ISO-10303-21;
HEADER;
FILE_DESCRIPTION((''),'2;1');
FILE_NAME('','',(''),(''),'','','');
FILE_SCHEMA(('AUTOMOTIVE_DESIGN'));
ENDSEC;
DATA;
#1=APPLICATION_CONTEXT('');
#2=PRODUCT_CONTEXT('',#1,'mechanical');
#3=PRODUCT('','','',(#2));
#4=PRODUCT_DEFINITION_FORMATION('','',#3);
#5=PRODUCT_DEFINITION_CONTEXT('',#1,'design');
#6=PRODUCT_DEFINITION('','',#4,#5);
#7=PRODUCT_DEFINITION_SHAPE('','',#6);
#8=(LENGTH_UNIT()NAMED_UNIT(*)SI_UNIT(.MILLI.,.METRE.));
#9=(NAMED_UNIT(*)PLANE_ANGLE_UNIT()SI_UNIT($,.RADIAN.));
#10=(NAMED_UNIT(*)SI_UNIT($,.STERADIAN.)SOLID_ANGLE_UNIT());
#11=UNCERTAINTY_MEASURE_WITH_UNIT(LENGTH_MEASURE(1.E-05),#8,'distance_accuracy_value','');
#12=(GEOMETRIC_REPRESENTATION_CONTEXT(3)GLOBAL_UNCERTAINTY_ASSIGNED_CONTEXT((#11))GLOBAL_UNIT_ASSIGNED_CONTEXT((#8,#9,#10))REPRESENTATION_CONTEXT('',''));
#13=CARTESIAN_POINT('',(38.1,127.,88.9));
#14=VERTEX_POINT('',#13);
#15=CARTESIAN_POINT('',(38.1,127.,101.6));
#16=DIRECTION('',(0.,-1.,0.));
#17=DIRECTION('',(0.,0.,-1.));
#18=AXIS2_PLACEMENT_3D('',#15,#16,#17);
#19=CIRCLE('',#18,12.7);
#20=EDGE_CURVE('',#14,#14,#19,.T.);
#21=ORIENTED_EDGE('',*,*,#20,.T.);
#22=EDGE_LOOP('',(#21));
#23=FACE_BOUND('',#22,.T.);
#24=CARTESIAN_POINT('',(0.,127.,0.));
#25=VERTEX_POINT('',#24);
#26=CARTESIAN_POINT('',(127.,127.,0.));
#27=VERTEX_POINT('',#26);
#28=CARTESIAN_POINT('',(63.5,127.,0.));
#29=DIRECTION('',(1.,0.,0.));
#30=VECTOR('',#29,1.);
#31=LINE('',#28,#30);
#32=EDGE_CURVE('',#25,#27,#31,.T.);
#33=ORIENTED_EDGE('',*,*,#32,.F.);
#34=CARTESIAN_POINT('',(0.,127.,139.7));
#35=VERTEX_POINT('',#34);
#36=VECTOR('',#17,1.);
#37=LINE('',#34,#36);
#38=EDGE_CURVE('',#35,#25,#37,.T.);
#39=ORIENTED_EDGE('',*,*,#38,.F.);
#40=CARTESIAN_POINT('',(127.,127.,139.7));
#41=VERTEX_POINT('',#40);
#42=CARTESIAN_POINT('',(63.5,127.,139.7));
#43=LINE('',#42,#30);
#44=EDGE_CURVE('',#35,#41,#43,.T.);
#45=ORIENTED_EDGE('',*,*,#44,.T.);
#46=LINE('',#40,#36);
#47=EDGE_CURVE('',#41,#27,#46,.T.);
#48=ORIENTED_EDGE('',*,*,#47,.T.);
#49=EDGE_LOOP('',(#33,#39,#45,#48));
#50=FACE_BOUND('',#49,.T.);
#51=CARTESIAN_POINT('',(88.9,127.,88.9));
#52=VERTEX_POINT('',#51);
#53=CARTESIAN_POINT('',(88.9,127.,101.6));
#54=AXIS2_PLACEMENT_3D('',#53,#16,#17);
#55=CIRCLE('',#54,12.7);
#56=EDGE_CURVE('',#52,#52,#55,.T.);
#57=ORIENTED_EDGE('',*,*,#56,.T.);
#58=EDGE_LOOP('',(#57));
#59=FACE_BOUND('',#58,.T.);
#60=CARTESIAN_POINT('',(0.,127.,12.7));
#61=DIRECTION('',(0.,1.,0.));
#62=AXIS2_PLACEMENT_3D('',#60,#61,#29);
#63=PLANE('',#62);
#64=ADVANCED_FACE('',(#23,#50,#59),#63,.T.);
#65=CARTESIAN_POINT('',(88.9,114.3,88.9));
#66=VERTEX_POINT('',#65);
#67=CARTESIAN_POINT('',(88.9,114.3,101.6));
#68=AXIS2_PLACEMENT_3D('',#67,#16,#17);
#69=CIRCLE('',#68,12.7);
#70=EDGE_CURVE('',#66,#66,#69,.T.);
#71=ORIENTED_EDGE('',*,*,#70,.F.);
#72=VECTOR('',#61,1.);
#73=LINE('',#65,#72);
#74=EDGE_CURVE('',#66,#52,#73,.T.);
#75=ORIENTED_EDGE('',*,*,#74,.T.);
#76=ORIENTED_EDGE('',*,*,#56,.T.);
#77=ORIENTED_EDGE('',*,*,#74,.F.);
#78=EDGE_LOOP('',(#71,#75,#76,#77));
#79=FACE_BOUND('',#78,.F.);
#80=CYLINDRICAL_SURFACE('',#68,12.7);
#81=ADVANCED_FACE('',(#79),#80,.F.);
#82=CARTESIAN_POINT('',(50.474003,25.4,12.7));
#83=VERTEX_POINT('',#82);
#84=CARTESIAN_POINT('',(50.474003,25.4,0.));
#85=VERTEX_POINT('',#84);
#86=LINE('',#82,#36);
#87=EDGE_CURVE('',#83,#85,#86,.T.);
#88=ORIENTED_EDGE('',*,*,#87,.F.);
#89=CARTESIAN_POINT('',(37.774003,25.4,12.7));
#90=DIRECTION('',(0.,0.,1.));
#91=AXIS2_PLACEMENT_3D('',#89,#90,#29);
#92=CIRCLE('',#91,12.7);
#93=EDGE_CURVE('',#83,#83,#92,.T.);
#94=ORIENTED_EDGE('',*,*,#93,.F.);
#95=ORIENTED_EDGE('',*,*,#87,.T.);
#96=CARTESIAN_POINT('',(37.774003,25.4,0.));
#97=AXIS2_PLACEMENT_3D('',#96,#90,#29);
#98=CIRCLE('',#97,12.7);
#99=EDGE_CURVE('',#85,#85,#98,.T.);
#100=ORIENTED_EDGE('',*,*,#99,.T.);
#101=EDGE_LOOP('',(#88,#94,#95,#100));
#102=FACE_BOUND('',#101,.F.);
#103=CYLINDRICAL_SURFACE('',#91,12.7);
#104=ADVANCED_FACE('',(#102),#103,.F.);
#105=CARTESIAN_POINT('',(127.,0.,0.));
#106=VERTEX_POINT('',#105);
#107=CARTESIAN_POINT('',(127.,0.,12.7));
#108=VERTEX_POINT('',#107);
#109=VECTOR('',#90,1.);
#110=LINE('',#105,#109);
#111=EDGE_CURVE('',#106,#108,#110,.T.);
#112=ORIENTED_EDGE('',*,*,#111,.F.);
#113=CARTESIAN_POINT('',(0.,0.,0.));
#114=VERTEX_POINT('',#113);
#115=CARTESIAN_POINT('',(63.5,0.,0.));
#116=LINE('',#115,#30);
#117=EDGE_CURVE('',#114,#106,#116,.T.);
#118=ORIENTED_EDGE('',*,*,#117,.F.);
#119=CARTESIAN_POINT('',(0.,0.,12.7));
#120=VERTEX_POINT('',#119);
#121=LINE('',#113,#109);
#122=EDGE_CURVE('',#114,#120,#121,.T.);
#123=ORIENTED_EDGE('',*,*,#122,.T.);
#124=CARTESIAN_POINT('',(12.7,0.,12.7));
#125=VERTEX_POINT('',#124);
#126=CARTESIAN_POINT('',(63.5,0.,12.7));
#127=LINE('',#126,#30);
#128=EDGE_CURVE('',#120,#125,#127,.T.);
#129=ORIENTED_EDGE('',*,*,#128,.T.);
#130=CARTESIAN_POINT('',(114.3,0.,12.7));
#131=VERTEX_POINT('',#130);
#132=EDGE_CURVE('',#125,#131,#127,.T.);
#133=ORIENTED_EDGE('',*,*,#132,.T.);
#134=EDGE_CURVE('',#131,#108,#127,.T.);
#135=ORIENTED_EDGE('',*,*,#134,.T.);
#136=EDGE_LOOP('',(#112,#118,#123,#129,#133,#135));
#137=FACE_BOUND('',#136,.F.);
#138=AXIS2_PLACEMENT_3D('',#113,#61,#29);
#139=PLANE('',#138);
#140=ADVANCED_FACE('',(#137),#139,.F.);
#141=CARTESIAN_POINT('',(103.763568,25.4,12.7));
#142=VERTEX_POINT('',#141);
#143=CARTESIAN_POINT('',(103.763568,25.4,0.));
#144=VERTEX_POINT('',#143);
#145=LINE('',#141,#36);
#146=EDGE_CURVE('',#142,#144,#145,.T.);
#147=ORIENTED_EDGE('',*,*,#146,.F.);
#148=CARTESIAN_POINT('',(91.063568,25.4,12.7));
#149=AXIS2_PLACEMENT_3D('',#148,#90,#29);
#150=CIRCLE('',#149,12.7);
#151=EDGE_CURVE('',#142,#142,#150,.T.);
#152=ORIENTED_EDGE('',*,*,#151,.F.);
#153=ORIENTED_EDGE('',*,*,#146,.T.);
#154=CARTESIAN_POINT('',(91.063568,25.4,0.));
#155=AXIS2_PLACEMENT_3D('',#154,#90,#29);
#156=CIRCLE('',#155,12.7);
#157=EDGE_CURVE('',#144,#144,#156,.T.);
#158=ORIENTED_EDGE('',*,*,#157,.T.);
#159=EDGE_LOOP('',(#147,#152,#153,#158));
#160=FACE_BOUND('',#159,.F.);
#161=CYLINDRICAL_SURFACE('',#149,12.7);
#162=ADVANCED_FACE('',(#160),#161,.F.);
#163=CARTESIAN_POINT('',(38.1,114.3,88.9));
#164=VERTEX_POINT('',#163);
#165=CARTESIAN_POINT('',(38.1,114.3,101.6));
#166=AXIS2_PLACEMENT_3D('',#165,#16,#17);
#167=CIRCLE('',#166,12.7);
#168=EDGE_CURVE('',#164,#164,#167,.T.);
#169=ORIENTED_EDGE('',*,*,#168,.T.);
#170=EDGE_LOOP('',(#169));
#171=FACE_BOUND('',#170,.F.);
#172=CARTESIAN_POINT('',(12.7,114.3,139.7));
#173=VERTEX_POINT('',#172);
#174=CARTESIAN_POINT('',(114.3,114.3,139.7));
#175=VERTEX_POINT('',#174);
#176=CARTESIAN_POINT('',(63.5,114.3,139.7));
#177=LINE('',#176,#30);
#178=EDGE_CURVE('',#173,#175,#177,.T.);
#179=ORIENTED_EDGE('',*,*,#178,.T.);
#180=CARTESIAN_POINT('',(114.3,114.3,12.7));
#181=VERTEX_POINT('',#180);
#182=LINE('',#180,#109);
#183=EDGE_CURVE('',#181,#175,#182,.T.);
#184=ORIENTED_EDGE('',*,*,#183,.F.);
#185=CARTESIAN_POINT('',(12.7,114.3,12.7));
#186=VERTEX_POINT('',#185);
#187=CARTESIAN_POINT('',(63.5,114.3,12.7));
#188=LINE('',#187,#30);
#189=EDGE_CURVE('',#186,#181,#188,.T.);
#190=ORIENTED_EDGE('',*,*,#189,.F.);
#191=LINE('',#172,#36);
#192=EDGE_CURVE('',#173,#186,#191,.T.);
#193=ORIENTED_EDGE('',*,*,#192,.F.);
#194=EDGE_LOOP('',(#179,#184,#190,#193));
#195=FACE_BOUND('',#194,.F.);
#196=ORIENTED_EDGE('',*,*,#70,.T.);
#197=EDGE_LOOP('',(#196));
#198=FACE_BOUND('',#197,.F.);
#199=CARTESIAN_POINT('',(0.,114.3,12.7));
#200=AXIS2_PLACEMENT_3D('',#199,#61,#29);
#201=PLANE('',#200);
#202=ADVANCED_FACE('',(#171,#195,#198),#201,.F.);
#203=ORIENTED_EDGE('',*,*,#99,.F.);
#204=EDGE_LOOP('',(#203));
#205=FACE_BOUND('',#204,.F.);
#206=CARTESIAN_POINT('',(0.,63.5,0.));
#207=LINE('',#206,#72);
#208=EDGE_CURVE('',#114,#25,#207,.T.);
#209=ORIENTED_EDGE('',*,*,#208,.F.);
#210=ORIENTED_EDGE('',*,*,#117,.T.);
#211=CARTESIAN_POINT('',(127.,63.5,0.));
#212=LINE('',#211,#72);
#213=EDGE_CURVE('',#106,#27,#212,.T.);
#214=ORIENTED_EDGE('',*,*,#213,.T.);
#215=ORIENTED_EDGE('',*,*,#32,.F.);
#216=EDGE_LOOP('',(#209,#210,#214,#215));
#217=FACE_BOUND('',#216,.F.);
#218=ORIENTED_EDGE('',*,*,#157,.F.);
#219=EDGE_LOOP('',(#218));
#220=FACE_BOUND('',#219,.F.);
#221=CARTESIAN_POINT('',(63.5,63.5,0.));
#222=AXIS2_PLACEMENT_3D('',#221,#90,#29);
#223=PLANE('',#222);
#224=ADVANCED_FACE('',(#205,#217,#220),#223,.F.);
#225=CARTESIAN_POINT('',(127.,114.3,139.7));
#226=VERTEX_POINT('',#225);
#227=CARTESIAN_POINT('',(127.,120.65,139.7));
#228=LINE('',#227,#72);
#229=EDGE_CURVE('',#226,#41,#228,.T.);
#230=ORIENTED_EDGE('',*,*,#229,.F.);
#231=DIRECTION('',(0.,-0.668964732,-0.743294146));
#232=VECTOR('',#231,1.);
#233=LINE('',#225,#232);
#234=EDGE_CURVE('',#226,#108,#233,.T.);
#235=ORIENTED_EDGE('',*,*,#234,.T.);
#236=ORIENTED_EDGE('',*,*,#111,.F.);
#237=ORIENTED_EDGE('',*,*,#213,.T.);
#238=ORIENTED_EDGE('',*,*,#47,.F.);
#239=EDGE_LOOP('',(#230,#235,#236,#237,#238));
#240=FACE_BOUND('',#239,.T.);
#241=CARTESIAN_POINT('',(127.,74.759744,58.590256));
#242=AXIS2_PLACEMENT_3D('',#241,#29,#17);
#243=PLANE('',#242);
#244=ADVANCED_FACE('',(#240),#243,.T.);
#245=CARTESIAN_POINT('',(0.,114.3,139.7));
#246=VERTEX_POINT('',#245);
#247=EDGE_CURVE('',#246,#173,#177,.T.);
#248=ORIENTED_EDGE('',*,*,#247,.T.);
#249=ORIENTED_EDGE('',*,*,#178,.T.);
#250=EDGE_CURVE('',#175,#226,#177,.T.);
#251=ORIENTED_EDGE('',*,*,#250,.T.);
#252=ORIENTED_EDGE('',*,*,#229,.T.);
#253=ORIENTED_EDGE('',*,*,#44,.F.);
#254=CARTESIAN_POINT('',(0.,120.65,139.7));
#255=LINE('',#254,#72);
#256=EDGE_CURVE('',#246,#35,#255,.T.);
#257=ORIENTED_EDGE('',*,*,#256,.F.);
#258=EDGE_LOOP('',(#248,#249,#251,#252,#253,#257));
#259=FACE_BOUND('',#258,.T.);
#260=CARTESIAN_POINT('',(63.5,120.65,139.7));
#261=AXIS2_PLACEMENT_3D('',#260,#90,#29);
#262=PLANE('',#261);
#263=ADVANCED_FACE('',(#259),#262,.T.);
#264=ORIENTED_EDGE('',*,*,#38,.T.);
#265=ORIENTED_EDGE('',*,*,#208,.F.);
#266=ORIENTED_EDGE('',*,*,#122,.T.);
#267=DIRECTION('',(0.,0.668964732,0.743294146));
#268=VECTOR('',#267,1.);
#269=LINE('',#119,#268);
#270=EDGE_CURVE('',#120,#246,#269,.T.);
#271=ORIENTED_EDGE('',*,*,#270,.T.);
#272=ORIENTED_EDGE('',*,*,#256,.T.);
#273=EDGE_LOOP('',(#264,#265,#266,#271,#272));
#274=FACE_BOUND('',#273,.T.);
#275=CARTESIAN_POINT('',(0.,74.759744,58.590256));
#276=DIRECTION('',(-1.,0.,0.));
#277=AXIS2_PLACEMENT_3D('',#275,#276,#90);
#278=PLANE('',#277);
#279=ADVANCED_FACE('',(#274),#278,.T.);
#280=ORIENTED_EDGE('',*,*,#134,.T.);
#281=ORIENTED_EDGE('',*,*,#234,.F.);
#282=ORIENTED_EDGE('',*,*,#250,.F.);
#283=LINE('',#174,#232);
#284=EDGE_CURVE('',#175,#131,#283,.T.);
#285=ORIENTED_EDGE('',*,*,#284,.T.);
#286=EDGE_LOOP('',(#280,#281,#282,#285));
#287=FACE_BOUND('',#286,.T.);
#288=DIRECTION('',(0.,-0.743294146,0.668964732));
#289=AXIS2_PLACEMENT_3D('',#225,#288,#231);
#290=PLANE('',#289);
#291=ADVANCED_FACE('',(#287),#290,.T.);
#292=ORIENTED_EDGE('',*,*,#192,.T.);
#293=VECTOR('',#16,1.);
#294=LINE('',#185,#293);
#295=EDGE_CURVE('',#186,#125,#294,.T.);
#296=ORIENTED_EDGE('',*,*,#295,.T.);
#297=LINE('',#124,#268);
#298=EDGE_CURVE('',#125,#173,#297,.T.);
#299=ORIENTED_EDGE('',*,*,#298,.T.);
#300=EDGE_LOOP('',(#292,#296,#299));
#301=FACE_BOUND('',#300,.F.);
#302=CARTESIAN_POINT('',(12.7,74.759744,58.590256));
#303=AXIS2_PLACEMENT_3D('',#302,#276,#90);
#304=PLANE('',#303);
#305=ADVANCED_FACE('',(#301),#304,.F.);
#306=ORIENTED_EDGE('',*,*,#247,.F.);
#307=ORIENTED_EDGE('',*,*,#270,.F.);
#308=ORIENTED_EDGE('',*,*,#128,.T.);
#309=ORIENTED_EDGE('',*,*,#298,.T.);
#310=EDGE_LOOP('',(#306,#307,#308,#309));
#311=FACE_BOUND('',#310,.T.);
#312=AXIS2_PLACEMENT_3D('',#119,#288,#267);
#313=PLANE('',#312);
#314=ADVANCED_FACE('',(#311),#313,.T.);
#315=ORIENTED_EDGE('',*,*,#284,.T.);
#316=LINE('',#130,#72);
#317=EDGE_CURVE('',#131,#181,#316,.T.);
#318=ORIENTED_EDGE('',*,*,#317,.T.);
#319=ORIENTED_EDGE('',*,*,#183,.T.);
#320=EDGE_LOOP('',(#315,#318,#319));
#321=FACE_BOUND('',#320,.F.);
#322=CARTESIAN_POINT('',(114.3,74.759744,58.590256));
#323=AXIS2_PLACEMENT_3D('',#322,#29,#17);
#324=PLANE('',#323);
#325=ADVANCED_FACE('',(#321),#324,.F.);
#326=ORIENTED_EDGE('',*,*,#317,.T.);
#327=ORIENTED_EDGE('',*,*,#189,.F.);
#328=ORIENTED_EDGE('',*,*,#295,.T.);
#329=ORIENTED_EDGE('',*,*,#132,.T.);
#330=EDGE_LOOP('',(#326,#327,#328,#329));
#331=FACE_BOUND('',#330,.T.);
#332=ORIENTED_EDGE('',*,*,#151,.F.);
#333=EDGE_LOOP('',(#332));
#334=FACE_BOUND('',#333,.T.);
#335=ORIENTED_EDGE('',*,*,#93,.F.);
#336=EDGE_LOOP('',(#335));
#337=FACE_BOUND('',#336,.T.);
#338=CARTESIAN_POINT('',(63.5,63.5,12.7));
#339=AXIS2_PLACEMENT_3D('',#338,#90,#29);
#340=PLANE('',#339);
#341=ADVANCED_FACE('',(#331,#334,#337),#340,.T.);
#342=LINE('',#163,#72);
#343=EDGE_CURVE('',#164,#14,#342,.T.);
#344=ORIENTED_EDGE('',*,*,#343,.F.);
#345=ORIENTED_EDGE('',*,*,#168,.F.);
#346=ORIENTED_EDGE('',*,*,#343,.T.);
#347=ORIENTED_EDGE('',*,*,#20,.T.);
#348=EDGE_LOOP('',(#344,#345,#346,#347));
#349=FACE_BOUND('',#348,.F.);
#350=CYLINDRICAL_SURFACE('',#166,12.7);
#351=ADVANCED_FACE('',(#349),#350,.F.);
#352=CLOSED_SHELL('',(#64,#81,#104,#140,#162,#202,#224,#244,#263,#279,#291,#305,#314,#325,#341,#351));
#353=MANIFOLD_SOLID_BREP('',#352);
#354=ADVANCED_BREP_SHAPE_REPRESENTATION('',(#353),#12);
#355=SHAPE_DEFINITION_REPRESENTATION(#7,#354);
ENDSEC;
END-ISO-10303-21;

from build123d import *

# Parameters (mm, degrees)
BASE_PLATE_SKETCH_W      = 127
BASE_PLATE_SKETCH_H      = 127
BASE_PLATE_DEPTH         = 12.7
UPRIGHT_WALL_SKETCH_W    = 127
UPRIGHT_WALL_SKETCH_H    = 12.7
UPRIGHT_WALL_DEPTH       = 127
GUSSET_1_DEPTH           = 12.7
GUSSET_2_DEPTH           = 12.7
MOUNTING_HOLE_1_SKETCH_R = 12.7
MOUNTING_HOLE_1_DEPTH    = 12.7
MOUNTING_HOLE_2_SKETCH_R = 12.7
MOUNTING_HOLE_2_DEPTH    = 12.7
MOUNTING_HOLE_3_SKETCH_R = 12.7
MOUNTING_HOLE_3_DEPTH    = 12.7
MOUNTING_HOLE_4_SKETCH_R = 12.7
MOUNTING_HOLE_4_DEPTH    = 12.7


with BuildPart() as part:
    # Base Plate Sketch → Base Plate (new body)
    with BuildSketch(Plane.XY):
        with Locations((63.5, 63.5)):
            Rectangle(BASE_PLATE_SKETCH_W, BASE_PLATE_SKETCH_H)
    extrude(amount=BASE_PLATE_DEPTH)

    # Upright Wall Sketch → Upright Wall (add)
    with BuildSketch(Plane.XY.offset(12.7)):
        with Locations((63.5, 120.65)):
            Rectangle(UPRIGHT_WALL_SKETCH_W, UPRIGHT_WALL_SKETCH_H)
    extrude(amount=UPRIGHT_WALL_DEPTH)

    # Gusset 1 Sketch → Gusset 1 (add)
    with BuildSketch(Plane.ZY):
        Polygon((12.7, 0), (139.7, 114.3), (12.7, 114.3), align=None)
    extrude(amount=-GUSSET_1_DEPTH)

    # Gusset 2 Sketch → Gusset 2 (add)
    with BuildSketch(Plane(origin=(127, 0, 0), x_dir=(0, 0, -1), z_dir=(1, 0, 0))):
        Polygon((-12.7, 0), (-12.7, 114.3), (-139.7, 114.3), align=None)
    extrude(amount=-GUSSET_2_DEPTH)

    # Mounting Hole 1 Sketch → Mounting Hole 1 (cut)
    with BuildSketch(Plane.XZ.offset(-114.3)):
        with Locations(Location((38.1, 101.6, 0), (0, 0, 270))):
            Circle(MOUNTING_HOLE_1_SKETCH_R)
    extrude(amount=-MOUNTING_HOLE_1_DEPTH, mode=Mode.SUBTRACT)

    # Mounting Hole 2 Sketch → Mounting Hole 2 (cut)
    with BuildSketch(Plane.XZ.offset(-114.3)):
        with Locations(Location((88.9, 101.6, 0), (0, 0, 270))):
            Circle(MOUNTING_HOLE_2_SKETCH_R)
    extrude(amount=-MOUNTING_HOLE_2_DEPTH, mode=Mode.SUBTRACT)

    # Mounting Hole 3 Sketch → Mounting Hole 3 (cut)
    with BuildSketch(Plane.XY.offset(12.7)):
        with Locations((37.774003387, 25.4)):
            Circle(MOUNTING_HOLE_3_SKETCH_R)
    extrude(amount=-MOUNTING_HOLE_3_DEPTH, mode=Mode.SUBTRACT)

    # Mounting Hole 4 Sketch → Mounting Hole 4 (cut)
    with BuildSketch(Plane.XY.offset(12.7)):
        with Locations((91.0635678, 25.4)):
            Circle(MOUNTING_HOLE_4_SKETCH_R)
    extrude(amount=-MOUNTING_HOLE_4_DEPTH, mode=Mode.SUBTRACT)


solid = part.part
